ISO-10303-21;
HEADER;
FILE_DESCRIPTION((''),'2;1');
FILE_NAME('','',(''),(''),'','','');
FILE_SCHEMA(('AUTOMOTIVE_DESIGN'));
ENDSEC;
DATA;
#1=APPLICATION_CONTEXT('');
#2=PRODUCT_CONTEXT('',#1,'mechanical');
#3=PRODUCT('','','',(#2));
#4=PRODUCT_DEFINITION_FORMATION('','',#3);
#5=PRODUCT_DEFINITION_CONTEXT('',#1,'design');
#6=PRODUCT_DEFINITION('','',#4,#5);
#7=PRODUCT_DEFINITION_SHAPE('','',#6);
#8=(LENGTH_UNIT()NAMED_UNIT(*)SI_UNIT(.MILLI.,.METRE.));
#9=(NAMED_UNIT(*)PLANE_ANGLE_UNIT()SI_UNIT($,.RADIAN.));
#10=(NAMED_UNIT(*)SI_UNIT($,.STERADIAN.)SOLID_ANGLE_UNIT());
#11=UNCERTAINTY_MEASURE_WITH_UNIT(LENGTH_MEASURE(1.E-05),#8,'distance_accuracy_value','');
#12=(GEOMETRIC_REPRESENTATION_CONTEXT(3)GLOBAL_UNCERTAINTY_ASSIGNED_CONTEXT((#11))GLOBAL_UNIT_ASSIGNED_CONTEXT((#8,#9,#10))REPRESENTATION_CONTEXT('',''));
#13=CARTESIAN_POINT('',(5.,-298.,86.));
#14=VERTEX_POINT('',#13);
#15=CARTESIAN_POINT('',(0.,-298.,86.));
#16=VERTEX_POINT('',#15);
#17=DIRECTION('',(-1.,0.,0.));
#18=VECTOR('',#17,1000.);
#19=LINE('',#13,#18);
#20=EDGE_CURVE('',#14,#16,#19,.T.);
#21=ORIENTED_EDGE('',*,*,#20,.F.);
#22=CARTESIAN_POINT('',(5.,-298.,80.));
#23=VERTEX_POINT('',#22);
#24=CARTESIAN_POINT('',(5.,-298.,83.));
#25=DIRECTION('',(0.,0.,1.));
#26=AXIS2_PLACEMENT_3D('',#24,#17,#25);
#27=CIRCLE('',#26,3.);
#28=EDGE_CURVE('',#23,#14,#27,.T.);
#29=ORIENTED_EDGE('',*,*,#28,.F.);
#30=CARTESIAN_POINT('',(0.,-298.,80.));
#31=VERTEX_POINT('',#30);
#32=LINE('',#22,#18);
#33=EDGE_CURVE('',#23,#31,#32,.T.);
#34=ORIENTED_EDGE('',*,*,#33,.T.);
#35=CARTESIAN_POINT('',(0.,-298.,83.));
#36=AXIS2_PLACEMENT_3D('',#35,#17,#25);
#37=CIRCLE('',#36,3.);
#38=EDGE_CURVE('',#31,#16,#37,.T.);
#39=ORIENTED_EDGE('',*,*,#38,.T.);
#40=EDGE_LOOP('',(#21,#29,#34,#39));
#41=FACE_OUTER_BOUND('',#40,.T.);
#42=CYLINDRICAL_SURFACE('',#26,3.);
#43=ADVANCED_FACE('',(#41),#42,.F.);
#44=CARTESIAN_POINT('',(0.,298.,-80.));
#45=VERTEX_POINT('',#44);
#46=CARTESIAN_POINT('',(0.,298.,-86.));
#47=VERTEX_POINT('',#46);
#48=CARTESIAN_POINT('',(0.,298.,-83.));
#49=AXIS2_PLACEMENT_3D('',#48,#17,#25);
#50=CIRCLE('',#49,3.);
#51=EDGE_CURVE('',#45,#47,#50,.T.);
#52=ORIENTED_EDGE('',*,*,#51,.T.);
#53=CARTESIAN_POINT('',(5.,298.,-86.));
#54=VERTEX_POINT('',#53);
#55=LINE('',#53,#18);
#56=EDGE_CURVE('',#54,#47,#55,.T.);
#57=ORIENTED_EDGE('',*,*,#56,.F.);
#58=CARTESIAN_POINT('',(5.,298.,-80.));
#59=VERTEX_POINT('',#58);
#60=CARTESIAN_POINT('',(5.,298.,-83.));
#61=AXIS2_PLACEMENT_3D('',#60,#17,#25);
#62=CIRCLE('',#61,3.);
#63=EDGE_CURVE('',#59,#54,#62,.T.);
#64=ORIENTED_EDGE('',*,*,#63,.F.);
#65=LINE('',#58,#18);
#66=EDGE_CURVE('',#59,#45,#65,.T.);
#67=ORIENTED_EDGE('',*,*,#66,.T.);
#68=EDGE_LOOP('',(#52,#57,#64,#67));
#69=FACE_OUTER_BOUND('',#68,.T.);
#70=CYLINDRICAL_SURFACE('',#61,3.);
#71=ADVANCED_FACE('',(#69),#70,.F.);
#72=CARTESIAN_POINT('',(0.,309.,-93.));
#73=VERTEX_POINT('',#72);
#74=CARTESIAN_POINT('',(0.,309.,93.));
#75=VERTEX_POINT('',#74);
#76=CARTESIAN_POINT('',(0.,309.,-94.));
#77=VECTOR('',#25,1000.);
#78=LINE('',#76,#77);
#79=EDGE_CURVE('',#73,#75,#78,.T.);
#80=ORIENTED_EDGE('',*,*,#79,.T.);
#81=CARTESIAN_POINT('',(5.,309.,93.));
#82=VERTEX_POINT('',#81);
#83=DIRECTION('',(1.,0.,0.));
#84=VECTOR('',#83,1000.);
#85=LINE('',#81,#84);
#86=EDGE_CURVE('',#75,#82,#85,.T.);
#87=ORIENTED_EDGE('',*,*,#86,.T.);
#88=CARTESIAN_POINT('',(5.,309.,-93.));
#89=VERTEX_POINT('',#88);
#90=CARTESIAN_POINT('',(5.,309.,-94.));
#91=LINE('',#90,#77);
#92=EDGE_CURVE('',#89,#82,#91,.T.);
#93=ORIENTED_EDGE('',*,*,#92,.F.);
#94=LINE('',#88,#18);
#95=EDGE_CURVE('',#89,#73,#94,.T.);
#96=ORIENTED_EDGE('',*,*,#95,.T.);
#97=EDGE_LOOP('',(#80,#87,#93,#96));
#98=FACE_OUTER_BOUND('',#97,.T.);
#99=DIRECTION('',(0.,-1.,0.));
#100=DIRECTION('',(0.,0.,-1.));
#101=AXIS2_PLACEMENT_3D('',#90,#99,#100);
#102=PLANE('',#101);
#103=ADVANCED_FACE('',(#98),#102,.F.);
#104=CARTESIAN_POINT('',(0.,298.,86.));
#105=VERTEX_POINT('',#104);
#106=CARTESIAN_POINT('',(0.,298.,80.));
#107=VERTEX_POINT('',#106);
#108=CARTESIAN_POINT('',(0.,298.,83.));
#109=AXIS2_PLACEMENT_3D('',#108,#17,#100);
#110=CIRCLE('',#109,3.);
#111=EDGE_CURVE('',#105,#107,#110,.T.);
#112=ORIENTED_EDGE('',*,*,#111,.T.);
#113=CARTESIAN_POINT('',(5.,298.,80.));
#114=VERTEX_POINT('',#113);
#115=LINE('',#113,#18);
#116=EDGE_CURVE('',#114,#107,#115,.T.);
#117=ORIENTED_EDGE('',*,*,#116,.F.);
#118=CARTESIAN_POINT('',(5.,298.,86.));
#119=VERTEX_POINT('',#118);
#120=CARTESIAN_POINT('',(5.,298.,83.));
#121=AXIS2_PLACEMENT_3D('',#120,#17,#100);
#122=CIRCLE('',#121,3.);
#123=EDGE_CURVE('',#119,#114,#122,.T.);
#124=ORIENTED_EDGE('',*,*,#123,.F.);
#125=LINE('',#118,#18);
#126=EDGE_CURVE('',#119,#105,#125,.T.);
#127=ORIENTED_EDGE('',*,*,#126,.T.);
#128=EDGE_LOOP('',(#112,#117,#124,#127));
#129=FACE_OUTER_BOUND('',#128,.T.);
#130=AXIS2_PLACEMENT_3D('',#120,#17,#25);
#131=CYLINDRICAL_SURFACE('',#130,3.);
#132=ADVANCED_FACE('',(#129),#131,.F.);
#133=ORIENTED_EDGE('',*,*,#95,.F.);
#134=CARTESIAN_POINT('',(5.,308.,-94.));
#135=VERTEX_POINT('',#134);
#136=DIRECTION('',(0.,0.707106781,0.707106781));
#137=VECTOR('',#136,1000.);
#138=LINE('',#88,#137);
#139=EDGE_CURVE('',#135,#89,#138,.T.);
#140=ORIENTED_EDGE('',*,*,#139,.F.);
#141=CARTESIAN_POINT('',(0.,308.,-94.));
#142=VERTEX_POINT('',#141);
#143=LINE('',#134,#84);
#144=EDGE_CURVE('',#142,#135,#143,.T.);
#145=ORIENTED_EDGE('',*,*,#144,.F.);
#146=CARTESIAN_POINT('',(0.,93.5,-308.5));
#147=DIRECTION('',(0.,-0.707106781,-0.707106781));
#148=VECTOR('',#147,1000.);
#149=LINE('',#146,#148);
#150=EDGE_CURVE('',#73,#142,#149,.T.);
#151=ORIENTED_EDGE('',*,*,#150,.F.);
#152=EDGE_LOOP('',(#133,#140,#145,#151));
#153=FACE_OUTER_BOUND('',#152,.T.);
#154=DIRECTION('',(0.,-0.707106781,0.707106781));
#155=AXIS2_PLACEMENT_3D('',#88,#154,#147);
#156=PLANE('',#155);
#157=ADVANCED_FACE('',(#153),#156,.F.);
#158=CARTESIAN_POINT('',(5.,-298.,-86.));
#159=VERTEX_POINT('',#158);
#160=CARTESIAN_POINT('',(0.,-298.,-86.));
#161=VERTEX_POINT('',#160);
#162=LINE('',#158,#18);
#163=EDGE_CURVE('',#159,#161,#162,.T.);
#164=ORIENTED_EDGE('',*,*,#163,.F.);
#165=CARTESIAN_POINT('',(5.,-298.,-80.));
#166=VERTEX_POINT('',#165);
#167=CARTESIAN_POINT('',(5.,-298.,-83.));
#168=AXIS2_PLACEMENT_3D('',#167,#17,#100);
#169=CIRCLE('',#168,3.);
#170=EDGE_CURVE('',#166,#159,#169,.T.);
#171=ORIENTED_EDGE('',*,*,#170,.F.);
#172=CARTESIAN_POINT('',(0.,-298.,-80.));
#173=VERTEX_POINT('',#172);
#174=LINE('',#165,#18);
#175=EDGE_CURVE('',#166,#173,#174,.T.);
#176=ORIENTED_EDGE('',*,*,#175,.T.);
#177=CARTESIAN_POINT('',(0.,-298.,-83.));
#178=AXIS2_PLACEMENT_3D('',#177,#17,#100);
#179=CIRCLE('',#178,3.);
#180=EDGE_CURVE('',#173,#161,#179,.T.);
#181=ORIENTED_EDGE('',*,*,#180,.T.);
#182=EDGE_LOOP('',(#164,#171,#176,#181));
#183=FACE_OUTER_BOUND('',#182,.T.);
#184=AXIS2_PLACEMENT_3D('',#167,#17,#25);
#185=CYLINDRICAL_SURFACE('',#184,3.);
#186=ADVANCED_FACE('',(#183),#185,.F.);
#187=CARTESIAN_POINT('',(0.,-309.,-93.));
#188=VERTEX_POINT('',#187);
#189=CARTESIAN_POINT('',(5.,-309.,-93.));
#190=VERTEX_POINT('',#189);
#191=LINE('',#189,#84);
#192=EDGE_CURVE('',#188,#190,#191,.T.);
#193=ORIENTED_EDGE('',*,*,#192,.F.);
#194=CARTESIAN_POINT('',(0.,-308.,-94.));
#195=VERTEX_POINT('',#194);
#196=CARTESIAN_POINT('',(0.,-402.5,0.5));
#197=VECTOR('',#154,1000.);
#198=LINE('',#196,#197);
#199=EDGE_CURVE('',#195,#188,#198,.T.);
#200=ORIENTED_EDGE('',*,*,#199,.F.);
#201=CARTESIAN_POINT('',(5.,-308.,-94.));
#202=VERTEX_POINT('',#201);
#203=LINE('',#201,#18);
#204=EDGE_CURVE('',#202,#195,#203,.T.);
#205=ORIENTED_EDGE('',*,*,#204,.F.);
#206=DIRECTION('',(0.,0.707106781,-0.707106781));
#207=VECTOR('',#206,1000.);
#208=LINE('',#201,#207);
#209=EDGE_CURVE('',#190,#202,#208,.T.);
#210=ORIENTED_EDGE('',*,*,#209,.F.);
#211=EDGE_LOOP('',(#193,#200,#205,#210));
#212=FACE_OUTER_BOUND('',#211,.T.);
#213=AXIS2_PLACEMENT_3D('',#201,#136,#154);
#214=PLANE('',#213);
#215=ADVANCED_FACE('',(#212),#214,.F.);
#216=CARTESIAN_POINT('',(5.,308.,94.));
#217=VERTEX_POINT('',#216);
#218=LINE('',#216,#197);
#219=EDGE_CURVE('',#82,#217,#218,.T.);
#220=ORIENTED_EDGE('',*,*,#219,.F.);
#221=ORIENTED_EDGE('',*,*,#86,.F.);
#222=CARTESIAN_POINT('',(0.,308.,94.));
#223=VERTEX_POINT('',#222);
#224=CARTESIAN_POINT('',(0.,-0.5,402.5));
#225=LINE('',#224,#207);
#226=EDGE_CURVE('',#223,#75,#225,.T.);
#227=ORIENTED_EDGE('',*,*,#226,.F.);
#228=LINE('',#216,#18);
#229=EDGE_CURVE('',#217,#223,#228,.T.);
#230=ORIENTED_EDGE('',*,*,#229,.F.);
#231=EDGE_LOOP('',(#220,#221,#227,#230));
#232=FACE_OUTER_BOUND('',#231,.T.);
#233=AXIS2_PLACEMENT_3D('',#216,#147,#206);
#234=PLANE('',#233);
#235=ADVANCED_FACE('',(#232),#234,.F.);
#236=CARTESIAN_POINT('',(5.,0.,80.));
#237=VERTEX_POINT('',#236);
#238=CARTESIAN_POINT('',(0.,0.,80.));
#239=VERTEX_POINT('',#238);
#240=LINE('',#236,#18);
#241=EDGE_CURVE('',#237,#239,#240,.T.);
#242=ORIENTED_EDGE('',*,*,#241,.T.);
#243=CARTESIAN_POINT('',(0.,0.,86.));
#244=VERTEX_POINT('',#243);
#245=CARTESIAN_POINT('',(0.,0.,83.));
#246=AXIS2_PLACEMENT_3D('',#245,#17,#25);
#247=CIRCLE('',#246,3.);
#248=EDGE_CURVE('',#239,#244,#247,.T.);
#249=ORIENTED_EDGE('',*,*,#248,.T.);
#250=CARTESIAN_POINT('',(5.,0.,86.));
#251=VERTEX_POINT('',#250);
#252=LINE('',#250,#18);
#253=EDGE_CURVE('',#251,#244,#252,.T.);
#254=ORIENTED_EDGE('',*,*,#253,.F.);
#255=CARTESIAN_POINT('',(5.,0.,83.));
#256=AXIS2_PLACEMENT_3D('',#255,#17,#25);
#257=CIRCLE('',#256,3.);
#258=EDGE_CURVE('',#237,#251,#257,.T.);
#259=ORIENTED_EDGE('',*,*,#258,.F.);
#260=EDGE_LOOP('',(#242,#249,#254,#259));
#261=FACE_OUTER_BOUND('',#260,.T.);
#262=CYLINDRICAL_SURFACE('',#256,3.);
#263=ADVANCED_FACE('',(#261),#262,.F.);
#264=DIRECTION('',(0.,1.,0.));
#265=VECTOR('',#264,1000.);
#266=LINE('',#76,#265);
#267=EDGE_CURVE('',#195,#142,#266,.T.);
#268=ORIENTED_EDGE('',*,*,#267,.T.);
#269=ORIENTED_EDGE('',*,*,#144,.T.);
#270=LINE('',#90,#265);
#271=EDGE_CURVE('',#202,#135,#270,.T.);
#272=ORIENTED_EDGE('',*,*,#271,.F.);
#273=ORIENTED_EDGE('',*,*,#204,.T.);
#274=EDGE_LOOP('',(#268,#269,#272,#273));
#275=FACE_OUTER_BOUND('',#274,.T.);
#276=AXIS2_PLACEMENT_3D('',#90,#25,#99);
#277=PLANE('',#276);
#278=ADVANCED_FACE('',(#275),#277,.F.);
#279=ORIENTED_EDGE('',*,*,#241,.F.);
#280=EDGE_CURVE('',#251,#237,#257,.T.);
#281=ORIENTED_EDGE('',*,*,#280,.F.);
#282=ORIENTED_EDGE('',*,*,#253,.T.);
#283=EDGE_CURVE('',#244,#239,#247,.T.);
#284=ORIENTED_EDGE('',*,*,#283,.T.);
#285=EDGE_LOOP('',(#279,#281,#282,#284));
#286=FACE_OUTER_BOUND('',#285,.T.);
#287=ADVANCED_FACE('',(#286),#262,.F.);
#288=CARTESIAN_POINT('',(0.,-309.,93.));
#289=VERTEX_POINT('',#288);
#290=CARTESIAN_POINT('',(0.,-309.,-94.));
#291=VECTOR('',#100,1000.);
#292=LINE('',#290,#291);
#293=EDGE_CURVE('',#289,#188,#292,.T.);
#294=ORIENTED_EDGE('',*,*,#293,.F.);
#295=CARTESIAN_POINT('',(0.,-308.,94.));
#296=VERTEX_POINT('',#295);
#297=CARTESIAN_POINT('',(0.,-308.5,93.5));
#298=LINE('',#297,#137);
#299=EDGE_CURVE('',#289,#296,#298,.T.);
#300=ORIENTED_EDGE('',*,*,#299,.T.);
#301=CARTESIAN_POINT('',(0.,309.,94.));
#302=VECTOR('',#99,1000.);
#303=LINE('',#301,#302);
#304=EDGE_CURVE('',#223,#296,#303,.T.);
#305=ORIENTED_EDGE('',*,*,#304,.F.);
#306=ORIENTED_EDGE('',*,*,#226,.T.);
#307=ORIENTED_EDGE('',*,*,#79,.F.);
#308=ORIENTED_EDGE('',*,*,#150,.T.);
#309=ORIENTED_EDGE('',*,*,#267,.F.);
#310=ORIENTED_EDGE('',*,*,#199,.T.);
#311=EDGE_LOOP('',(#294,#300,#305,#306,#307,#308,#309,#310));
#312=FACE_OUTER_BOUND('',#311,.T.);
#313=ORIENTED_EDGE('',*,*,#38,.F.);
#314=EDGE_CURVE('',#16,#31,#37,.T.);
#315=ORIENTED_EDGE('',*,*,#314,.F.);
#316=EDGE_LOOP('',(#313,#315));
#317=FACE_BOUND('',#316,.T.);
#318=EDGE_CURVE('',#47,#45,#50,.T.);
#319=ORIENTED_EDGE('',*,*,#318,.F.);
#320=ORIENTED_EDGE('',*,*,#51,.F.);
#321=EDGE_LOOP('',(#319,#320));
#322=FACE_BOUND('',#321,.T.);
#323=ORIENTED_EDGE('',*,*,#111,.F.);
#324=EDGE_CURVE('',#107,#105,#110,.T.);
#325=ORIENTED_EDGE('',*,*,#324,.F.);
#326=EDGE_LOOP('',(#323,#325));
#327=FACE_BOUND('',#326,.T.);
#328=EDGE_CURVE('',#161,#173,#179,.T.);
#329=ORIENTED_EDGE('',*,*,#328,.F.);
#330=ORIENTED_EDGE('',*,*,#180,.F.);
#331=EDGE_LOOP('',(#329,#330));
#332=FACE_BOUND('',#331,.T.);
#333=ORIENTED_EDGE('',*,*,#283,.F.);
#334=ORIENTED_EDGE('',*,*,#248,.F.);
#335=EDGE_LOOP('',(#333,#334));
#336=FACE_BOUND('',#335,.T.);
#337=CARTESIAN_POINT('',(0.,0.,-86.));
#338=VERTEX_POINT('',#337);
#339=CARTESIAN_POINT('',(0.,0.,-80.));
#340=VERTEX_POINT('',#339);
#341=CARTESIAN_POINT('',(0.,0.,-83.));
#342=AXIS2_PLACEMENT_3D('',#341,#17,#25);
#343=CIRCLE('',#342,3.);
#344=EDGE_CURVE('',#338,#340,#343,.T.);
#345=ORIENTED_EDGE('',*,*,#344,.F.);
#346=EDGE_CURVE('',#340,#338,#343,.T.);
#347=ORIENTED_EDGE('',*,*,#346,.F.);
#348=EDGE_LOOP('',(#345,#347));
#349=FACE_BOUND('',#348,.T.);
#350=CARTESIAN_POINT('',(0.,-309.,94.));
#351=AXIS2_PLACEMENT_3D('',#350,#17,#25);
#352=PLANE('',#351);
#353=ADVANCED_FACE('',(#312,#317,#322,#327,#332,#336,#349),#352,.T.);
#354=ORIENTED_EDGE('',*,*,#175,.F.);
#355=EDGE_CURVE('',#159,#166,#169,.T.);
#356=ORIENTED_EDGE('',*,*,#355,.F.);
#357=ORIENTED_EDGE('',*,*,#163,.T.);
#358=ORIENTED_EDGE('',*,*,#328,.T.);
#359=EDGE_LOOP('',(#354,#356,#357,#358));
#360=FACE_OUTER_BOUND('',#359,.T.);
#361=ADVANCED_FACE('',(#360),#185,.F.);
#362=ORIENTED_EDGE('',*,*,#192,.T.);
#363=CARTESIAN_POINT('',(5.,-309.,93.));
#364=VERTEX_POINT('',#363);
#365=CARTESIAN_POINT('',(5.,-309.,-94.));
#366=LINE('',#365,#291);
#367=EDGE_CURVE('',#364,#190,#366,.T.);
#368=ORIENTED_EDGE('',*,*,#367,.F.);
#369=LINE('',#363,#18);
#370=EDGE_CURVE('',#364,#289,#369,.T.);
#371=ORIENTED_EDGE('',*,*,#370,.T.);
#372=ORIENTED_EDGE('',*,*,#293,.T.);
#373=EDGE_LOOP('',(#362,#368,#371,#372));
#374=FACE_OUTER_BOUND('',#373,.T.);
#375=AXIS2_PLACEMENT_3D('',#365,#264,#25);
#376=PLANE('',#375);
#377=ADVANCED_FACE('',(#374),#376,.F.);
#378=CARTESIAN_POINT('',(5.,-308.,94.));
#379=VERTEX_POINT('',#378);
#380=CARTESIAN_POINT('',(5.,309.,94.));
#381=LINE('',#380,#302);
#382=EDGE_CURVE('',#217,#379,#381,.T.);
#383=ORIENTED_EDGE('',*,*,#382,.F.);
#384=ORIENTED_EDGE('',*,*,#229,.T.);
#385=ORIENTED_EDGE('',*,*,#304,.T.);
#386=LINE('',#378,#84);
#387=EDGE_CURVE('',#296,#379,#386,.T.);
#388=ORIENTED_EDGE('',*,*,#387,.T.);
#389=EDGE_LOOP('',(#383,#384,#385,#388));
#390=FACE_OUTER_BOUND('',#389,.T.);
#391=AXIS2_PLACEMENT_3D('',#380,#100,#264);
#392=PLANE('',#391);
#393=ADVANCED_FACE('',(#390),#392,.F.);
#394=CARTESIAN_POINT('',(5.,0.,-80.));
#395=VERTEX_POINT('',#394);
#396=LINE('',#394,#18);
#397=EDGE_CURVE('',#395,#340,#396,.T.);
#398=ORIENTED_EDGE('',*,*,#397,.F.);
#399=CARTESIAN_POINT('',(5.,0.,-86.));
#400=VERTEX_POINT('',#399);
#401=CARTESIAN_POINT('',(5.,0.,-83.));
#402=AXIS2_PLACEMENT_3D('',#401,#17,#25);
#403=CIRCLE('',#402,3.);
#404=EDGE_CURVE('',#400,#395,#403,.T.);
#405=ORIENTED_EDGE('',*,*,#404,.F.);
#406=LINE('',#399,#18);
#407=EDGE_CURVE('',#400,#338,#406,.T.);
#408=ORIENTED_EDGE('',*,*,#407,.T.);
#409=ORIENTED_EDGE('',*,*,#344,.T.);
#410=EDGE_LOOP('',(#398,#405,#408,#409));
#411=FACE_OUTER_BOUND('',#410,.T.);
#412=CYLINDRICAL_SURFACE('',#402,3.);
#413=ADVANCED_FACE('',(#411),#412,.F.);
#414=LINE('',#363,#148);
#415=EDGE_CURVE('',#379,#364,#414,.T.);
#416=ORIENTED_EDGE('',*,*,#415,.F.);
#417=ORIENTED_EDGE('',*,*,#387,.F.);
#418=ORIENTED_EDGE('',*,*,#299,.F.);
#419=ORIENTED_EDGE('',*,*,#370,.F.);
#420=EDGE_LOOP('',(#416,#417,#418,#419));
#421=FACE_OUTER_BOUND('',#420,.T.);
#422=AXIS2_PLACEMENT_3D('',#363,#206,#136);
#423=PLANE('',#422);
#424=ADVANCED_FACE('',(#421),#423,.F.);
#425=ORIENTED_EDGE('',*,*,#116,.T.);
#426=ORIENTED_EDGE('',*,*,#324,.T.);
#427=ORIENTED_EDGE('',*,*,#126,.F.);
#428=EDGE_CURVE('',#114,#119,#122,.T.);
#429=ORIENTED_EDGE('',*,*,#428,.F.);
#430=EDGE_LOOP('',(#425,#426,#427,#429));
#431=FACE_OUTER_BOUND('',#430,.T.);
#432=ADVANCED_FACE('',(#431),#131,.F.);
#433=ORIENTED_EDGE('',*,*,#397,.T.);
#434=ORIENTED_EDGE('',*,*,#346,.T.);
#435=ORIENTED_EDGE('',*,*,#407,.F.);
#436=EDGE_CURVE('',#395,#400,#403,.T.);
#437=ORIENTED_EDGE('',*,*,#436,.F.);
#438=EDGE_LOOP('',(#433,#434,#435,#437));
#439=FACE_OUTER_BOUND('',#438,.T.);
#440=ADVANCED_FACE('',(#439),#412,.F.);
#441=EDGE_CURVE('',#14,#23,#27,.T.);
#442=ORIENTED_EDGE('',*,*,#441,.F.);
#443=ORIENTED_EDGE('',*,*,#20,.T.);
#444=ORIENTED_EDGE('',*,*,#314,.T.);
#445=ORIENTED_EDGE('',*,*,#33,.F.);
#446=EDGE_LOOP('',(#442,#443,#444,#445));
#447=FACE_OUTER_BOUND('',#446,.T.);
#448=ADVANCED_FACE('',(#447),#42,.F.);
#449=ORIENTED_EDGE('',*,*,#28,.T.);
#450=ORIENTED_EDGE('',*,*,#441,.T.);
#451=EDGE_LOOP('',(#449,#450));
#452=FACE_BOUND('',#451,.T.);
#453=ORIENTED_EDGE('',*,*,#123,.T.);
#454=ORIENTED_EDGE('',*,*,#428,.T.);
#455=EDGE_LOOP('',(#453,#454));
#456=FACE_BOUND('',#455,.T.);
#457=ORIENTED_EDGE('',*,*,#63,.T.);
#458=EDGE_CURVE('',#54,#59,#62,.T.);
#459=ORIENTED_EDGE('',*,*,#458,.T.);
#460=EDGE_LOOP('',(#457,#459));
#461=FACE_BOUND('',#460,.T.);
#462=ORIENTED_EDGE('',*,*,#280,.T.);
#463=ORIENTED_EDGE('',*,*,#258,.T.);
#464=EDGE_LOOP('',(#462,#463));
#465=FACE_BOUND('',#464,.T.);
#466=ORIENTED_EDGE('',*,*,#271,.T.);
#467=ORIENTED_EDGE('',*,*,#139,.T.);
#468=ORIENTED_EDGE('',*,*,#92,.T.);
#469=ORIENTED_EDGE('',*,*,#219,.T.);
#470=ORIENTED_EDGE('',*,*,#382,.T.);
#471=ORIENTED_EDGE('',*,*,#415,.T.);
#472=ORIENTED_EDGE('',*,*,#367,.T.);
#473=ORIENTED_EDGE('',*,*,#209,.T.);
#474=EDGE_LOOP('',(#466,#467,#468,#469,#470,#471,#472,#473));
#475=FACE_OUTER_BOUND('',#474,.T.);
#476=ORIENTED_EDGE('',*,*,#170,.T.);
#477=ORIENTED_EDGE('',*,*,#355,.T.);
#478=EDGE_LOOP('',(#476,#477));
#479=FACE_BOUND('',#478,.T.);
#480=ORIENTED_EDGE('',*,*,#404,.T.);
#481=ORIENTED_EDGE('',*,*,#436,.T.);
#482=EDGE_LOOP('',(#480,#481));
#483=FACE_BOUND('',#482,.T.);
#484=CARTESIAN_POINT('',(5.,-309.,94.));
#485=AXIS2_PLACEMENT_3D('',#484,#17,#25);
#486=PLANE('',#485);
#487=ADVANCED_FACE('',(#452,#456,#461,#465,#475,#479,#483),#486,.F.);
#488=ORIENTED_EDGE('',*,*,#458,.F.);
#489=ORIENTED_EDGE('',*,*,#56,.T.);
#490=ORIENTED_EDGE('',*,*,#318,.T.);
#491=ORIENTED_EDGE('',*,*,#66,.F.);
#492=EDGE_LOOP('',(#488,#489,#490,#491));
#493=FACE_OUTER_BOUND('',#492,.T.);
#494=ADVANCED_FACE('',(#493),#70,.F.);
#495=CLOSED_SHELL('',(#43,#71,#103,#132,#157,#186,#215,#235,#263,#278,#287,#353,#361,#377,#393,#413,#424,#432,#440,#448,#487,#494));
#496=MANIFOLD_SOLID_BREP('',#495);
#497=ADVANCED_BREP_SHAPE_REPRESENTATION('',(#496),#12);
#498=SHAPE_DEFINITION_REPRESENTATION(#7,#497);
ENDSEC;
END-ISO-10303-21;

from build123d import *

# Parameters (mm, degrees)
SKETCH_1_W          = 188
SKETCH_1_H          = 618
EXTRUDE_1_DEPTH     = 5
CHAMFER_1_SIZE      = 1
SKETCH_2_R          = 3
CUT_EXTRUDE_1_DEPTH = 324.020123212


with BuildPart() as part:
    # 草图1 → 凸台-拉伸1 (new body)
    with BuildSketch(Plane(origin=(0, 0, 0), x_dir=(0, 0, -1), z_dir=(1, 0, 0))):
        Rectangle(SKETCH_1_W, SKETCH_1_H)
    extrude(amount=EXTRUDE_1_DEPTH)

    # 倒角1
    chamfer_1_edges = [part.edges().sort_by_distance(p)[0] for p in [
        (2.5, 309, 94),
        (2.5, 309, -94),
        (2.5, -309, -94),
        (2.5, -309, 94),
    ]]
    chamfer(chamfer_1_edges, length=CHAMFER_1_SIZE)

    # 草图2 → 切除-拉伸1 (cut, through all)
    with BuildSketch(Plane.ZY):
        with Locations((-83, 298)):
            Circle(SKETCH_2_R)
        with Locations(Location((-83, -298, 0), (0, 0, 180))):
            Circle(SKETCH_2_R)
        with Locations((83, -298)):
            Circle(SKETCH_2_R)
        with Locations(Location((83, 298, 0), (0, 0, 180))):
            Circle(SKETCH_2_R)
        with Locations((83, 0)):
            Circle(SKETCH_2_R)
        with Locations((-83, 0)):
            Circle(SKETCH_2_R)
    extrude(amount=-CUT_EXTRUDE_1_DEPTH, mode=Mode.SUBTRACT)


solid = part.part
